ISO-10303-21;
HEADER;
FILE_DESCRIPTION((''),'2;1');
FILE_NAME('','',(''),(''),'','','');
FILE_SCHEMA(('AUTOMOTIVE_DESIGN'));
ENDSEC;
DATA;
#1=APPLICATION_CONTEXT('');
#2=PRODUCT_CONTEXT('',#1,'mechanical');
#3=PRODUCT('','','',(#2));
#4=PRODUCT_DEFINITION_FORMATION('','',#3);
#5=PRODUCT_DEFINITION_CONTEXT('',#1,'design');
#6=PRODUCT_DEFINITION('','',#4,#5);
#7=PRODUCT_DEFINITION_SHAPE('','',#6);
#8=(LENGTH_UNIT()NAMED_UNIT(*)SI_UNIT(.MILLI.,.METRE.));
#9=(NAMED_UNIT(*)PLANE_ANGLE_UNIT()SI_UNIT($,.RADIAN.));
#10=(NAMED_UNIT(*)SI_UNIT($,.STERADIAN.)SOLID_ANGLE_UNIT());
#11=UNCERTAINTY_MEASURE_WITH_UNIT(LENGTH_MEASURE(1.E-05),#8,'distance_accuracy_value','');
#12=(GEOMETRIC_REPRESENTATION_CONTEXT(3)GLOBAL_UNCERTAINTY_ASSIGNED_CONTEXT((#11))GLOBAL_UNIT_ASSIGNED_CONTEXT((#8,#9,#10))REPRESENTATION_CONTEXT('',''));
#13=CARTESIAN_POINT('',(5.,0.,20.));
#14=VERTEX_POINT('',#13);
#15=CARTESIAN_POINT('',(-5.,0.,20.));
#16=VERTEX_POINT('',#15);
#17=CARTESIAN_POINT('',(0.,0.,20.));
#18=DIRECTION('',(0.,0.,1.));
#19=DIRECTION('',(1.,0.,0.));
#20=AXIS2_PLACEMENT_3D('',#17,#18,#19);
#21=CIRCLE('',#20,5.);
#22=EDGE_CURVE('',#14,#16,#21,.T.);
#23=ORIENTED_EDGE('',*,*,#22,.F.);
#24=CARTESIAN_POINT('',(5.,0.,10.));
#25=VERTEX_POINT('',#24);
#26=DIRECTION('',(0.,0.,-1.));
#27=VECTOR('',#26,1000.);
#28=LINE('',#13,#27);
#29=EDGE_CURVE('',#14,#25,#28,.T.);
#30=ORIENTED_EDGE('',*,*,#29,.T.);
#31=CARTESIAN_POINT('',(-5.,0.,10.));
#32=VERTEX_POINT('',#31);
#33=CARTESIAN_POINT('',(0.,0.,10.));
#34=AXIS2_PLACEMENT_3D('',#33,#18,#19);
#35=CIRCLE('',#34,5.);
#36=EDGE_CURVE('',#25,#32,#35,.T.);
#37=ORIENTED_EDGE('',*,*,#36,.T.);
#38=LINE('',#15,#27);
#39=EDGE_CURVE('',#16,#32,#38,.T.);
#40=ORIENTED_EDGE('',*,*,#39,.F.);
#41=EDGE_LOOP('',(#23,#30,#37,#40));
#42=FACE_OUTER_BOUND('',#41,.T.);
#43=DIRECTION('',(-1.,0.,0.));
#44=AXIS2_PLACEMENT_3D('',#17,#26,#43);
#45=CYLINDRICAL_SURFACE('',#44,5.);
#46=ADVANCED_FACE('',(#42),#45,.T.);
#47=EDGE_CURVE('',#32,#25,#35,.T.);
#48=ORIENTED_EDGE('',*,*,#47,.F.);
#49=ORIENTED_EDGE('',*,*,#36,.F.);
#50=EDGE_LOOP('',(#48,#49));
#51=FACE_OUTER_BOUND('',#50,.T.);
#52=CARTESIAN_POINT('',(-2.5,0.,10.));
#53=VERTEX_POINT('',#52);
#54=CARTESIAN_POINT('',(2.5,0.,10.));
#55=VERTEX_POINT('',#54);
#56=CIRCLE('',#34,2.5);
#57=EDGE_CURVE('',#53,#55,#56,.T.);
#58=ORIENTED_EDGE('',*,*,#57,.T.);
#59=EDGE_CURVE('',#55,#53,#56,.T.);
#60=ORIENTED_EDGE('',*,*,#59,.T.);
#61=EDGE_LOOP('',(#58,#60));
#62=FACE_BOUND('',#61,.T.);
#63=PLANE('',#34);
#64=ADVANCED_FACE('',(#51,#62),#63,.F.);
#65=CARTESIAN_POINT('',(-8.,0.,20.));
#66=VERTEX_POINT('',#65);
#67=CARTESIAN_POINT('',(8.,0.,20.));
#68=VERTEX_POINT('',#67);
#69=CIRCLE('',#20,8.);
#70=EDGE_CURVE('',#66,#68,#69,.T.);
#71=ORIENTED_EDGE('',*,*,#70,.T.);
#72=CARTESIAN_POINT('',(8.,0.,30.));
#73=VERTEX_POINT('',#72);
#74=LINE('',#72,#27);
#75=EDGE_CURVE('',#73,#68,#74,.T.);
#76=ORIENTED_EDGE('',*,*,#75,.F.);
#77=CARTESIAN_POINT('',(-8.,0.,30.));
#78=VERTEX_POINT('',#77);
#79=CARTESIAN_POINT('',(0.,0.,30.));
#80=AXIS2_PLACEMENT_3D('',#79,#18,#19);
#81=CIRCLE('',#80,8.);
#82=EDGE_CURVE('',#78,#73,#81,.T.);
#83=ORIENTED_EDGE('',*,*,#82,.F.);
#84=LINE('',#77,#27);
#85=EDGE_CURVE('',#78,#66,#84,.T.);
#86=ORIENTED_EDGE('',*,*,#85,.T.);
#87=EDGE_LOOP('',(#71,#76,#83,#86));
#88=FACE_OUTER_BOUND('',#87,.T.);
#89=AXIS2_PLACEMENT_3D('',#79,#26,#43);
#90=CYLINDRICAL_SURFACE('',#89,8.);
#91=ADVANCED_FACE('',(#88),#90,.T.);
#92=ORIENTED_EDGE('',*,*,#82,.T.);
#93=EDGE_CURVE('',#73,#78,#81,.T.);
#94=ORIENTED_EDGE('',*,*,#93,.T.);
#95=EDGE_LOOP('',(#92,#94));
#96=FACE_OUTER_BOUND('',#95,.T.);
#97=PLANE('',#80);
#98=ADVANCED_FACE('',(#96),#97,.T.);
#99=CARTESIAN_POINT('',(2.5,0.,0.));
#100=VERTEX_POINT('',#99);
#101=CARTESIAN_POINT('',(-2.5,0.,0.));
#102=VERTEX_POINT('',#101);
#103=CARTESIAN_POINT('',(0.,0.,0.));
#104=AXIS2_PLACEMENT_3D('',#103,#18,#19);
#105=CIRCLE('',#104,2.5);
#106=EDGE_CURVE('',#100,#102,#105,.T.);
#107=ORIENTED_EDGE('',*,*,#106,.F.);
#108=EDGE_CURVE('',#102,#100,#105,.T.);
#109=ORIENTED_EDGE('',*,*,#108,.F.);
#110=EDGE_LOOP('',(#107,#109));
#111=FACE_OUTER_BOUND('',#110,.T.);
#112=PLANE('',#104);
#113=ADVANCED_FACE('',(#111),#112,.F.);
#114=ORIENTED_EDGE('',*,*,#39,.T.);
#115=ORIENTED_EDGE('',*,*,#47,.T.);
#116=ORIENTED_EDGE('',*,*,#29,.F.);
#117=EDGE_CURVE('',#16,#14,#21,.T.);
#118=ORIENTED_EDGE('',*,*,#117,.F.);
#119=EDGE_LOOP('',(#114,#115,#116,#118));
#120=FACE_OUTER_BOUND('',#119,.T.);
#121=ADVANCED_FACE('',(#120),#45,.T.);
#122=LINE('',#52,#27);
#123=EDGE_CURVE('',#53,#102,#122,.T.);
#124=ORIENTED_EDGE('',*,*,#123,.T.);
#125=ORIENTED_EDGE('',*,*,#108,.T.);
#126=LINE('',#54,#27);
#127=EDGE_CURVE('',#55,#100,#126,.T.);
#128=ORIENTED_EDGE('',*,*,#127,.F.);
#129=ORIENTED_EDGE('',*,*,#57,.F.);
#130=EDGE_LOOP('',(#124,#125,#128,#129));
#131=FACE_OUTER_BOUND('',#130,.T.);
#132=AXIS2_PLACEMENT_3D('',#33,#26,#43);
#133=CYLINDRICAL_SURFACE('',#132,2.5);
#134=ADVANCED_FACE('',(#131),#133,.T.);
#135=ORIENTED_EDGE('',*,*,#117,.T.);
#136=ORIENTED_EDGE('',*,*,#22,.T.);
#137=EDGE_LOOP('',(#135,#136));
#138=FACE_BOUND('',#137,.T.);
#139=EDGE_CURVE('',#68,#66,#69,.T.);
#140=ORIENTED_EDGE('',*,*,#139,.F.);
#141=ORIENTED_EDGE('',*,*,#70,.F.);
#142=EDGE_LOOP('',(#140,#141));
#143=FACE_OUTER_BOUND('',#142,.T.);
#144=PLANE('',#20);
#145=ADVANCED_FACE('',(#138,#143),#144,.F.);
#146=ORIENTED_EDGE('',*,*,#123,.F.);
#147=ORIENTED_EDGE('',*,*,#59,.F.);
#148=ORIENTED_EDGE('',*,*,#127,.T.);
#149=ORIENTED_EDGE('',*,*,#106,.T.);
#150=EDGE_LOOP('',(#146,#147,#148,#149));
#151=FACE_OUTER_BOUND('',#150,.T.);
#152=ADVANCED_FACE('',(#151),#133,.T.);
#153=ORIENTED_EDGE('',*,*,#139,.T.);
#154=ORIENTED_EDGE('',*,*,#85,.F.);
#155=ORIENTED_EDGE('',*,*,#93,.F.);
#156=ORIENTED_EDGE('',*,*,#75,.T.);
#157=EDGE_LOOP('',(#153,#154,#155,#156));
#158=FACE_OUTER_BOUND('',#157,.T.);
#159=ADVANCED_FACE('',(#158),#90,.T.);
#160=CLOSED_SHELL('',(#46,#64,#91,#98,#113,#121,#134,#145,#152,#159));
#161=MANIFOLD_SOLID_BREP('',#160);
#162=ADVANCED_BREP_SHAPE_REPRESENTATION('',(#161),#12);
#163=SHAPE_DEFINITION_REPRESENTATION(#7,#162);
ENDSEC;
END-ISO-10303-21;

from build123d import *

# Parameters (mm, degrees)
SKETCH1_R           = 2.5
BOSS_EXTRUDE1_DEPTH = 10
SKETCH2_R           = 5
BOSS_EXTRUDE2_DEPTH = 10
SKETCH3_R           = 8
BOSS_EXTRUDE3_DEPTH = 10


with BuildPart() as part:
    # Sketch1 → Boss-Extrude1 (new body)
    with BuildSketch(Plane.XY):
        Circle(SKETCH1_R)
    extrude(amount=BOSS_EXTRUDE1_DEPTH)

    # Sketch2 → Boss-Extrude2 (add)
    with BuildSketch(Plane.XY.offset(10)):
        Circle(SKETCH2_R)
    extrude(amount=BOSS_EXTRUDE2_DEPTH)

    # Sketch3 → Boss-Extrude3 (add)
    with BuildSketch(Plane.XY.offset(20)):
        Circle(SKETCH3_R)
    extrude(amount=BOSS_EXTRUDE3_DEPTH)


solid = part.part
